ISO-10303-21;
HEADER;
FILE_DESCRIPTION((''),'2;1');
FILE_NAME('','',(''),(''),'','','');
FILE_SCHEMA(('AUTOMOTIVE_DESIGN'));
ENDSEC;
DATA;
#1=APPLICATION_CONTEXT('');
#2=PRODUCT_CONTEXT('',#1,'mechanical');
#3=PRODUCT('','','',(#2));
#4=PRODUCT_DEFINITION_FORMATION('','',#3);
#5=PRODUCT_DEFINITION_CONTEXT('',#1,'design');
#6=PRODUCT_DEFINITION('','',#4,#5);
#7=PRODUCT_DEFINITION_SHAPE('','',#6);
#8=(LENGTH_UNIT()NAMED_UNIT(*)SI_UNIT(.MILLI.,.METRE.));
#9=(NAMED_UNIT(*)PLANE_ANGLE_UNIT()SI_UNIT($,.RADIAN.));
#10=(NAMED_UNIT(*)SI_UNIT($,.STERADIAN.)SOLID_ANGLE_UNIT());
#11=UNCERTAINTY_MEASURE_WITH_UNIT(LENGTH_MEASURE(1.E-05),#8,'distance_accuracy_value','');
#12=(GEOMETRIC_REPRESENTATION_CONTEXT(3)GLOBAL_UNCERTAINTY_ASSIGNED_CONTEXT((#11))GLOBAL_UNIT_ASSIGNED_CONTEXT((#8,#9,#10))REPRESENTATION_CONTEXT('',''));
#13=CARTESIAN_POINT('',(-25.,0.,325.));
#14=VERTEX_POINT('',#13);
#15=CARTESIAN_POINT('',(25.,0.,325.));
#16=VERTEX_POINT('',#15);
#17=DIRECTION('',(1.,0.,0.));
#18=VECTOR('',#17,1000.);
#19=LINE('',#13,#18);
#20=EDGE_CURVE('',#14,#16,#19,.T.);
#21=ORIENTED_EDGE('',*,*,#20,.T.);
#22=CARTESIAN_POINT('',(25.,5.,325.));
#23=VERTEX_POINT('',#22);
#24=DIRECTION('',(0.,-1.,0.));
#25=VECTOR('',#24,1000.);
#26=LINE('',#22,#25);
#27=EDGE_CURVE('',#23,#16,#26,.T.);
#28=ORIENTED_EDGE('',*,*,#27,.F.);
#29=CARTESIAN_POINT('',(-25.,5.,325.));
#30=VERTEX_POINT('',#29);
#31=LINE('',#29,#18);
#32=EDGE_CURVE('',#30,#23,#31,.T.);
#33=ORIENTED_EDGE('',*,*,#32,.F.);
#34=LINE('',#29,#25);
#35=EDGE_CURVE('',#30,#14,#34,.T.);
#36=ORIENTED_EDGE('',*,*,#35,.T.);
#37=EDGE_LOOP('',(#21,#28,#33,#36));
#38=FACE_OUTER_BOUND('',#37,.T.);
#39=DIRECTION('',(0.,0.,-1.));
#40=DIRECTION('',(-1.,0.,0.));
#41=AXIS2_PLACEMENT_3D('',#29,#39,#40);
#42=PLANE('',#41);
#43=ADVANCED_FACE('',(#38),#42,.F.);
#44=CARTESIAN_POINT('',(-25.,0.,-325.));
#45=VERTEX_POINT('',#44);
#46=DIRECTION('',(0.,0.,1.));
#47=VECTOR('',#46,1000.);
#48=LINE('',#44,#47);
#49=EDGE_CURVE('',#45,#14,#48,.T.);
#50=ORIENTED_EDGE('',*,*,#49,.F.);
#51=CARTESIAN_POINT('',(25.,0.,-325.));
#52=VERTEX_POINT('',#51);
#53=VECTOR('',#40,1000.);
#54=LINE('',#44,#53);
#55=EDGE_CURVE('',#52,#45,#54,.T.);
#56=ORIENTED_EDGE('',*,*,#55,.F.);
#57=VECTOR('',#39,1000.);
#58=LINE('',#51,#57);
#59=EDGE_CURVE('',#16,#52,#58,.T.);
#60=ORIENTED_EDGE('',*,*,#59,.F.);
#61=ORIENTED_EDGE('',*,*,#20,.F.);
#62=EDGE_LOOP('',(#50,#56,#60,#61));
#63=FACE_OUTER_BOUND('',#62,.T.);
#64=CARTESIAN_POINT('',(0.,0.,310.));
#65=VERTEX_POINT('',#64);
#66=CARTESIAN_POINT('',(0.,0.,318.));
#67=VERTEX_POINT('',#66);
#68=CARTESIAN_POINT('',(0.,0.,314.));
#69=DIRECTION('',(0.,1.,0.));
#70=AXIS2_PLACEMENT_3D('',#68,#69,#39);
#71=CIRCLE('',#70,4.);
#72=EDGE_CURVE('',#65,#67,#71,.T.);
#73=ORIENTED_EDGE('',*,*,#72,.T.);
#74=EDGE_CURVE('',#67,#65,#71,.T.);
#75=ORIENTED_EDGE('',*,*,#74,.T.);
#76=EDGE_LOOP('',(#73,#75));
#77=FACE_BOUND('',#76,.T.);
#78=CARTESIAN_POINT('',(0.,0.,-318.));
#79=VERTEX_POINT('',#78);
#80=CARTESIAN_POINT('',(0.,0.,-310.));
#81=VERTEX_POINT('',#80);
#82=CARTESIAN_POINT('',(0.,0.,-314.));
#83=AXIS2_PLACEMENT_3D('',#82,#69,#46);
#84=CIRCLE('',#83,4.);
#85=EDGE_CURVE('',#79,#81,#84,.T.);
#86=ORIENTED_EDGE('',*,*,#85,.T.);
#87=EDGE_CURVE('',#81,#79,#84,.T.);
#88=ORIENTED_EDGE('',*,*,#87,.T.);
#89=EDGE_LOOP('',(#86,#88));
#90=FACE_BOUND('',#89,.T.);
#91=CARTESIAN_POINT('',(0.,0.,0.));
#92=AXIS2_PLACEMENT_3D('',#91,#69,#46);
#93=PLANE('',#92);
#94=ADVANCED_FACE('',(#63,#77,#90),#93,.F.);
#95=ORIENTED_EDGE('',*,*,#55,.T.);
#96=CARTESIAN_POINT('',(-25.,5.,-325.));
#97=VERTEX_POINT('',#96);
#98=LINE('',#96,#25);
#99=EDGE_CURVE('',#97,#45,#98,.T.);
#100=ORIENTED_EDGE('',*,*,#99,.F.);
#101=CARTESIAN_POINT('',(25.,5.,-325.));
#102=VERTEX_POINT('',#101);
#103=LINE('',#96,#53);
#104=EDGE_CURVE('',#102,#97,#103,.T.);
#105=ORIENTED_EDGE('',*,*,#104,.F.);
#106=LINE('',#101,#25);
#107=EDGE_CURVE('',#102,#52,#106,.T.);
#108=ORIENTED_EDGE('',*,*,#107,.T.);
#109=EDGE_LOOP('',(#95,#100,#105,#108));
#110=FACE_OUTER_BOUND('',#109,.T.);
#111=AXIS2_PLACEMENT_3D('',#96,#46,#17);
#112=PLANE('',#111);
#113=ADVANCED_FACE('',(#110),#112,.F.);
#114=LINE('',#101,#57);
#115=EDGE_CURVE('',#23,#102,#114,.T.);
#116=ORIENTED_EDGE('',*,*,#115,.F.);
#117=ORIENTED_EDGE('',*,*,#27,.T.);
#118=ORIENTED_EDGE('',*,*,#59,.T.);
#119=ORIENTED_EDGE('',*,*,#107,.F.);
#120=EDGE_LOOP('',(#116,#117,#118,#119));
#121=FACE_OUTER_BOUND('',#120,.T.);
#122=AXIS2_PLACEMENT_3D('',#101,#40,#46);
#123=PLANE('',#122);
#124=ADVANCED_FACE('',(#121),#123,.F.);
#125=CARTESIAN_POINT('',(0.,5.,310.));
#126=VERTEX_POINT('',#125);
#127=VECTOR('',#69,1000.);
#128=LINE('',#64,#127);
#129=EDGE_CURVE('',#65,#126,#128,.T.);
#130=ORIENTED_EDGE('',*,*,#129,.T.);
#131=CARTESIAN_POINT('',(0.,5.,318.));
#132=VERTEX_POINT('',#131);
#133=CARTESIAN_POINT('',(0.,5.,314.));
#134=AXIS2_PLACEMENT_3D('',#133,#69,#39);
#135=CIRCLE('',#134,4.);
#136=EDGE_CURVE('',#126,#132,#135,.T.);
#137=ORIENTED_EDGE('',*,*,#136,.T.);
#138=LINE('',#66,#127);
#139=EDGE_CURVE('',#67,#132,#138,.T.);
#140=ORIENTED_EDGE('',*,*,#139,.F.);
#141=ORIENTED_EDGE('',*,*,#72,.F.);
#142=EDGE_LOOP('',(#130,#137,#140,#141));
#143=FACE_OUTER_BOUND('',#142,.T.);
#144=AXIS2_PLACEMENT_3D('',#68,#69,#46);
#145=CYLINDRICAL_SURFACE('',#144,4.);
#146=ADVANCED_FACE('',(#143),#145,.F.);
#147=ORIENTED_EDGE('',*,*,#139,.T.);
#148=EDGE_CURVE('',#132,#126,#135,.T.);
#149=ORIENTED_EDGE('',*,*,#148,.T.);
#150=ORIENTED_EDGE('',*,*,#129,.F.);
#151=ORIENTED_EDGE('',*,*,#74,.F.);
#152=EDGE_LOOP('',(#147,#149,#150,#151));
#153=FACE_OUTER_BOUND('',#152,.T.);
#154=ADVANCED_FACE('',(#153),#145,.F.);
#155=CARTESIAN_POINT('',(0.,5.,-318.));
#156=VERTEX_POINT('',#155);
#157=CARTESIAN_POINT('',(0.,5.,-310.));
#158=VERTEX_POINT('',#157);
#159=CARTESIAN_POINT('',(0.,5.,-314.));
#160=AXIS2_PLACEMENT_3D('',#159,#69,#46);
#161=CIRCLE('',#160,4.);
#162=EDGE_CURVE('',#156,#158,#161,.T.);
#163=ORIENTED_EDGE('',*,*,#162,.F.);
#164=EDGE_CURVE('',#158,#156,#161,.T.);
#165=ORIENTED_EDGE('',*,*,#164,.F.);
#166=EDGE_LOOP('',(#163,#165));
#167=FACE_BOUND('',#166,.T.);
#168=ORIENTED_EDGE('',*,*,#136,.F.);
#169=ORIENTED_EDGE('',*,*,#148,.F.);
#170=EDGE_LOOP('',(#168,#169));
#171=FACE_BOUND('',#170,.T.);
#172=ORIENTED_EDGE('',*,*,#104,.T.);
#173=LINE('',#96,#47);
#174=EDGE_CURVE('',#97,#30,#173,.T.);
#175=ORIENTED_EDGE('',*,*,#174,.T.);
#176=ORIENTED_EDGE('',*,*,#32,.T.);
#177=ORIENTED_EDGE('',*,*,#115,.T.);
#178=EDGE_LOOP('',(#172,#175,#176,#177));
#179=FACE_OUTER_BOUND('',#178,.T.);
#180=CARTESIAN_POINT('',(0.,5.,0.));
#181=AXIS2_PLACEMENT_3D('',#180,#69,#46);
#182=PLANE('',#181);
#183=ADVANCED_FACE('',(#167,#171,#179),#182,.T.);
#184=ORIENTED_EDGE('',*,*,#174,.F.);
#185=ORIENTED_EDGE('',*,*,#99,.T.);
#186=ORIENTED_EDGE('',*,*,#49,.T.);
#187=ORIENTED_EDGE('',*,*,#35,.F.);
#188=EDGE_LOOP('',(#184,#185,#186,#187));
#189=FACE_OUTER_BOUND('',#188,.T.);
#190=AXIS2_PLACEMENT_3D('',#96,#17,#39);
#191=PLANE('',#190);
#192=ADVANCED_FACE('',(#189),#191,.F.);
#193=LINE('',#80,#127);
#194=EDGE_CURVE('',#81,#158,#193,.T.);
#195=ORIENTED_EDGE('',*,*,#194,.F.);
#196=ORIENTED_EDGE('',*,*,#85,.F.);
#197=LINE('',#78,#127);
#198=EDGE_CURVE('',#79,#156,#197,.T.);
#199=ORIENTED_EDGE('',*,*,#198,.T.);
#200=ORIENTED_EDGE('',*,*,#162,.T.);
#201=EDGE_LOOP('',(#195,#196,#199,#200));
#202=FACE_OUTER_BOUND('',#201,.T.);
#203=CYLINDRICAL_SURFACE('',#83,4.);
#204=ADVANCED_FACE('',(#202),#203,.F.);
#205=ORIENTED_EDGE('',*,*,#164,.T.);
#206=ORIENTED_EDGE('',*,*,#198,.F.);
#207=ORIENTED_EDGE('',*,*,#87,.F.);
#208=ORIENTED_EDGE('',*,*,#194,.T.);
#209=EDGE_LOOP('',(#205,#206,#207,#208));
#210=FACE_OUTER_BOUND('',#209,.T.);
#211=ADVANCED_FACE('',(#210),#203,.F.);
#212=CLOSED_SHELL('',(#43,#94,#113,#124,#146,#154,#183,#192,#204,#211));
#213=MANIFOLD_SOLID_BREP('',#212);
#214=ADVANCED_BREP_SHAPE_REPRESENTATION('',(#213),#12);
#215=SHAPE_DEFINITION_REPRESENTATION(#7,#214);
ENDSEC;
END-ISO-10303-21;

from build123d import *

# Parameters (mm, degrees)
SKETCH_1_W          = 50
SKETCH_1_H          = 650
EXTRUDE_1_DEPTH     = 5
SKETCH_2_R          = 4
CUT_EXTRUDE_1_DEPTH = 326.998466254


with BuildPart() as part:
    # 草图1 → 凸台-拉伸1 (new body)
    with BuildSketch(Plane(origin=(0, 0, 0), x_dir=(1, 0, 0), z_dir=(0, 1, 0))):
        Rectangle(SKETCH_1_W, SKETCH_1_H)
    extrude(amount=EXTRUDE_1_DEPTH)

    # 草图2 → 切除-拉伸1 (cut, through all)
    with BuildSketch(Plane(origin=(0, 5, 0), x_dir=(1, 0, 0), z_dir=(0, 1, 0))):
        with Locations(Location((0, 314, 0), (0, 0, 270))):
            Circle(SKETCH_2_R)
        with Locations(Location((0, -314, 0), (0, 0, 90))):
            Circle(SKETCH_2_R)
    extrude(amount=-CUT_EXTRUDE_1_DEPTH, mode=Mode.SUBTRACT)


solid = part.part
